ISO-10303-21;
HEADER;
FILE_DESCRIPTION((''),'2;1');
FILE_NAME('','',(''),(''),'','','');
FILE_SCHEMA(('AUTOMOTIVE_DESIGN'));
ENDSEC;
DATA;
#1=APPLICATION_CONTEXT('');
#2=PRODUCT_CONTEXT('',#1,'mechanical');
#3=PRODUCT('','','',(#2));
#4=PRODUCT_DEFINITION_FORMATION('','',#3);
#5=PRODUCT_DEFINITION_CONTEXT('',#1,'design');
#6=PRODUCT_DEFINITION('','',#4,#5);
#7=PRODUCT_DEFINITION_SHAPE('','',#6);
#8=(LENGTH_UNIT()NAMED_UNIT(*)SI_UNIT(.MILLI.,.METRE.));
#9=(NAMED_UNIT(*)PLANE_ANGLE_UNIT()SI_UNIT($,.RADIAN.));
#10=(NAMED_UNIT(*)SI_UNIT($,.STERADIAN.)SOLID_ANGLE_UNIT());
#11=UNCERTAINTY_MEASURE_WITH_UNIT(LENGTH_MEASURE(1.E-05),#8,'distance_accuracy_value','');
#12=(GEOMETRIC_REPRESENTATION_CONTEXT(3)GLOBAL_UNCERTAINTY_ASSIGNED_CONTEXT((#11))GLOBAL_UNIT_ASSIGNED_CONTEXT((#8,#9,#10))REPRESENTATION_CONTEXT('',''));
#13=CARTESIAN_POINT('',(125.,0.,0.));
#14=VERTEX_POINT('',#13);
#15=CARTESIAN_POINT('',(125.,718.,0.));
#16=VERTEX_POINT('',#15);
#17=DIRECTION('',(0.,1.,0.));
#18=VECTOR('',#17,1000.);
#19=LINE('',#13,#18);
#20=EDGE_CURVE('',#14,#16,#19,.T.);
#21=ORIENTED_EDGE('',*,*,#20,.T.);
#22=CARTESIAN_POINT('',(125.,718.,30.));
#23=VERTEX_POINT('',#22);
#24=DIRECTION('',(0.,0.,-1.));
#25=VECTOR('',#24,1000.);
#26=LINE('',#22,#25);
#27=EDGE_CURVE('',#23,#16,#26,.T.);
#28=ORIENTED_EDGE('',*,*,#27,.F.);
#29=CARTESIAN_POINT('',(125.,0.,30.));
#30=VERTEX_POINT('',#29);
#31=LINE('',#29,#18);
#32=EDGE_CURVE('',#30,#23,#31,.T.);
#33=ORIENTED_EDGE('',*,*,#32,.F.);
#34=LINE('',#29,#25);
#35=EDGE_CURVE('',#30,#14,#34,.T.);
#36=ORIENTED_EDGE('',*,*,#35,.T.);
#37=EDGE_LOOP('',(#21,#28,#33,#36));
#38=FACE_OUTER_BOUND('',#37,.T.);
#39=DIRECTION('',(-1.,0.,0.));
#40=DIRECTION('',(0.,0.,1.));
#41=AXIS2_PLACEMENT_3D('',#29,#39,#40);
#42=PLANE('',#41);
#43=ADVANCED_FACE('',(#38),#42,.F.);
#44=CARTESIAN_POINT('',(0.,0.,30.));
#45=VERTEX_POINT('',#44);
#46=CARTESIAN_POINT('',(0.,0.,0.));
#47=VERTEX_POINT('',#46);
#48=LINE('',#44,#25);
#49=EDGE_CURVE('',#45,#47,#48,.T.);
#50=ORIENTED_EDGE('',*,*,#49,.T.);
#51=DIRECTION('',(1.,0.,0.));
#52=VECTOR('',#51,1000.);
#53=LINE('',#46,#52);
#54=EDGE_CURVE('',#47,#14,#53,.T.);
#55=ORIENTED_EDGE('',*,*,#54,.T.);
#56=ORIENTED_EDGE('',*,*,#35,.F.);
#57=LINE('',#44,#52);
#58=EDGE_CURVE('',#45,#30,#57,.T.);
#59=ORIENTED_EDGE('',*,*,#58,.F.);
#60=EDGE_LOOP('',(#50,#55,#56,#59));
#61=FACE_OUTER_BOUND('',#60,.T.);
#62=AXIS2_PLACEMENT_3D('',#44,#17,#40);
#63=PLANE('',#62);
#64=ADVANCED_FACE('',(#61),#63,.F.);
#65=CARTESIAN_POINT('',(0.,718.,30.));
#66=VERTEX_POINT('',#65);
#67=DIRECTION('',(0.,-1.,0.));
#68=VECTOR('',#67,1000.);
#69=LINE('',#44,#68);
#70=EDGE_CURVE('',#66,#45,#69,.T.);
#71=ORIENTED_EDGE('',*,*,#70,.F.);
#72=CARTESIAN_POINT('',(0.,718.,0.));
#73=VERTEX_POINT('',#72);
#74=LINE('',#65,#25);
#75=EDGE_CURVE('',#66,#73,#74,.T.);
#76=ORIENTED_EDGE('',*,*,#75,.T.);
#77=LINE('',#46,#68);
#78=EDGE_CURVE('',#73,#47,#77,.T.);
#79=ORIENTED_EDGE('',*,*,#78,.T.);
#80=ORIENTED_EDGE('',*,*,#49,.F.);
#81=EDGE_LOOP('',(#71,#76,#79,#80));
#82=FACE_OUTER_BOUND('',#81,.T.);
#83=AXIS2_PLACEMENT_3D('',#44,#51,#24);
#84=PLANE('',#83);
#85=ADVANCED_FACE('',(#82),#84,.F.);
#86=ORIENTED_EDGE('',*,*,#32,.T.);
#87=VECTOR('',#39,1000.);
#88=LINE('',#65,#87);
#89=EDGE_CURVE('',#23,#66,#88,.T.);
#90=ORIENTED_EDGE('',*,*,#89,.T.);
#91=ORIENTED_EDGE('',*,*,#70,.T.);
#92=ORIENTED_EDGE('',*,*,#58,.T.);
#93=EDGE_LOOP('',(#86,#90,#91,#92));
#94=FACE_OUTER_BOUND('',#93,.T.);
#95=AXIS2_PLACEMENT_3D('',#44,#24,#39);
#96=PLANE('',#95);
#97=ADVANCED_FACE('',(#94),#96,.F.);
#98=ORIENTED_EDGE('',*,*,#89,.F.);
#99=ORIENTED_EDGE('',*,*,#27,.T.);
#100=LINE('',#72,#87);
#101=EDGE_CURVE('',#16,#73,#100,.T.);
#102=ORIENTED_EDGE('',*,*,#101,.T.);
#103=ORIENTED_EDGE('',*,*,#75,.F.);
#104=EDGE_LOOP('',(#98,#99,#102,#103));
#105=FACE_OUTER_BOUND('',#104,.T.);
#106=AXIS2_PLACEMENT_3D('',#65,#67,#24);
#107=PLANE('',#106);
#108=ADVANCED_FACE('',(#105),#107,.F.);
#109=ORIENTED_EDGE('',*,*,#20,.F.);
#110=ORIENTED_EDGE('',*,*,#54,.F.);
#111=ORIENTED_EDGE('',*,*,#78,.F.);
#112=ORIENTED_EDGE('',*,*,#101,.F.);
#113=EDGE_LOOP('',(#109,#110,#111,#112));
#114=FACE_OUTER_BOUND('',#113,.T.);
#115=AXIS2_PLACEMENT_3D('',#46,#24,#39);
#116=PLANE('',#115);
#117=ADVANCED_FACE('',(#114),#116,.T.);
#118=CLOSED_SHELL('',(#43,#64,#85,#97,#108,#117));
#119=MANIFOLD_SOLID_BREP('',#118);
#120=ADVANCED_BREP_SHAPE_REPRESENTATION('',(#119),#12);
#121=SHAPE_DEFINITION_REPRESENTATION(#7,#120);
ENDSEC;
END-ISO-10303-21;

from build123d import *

# Parameters (mm, degrees)
SKETCH1_W           = 125
SKETCH1_H           = 718
BOSS_EXTRUDE1_DEPTH = 30


with BuildPart() as part:
    # Sketch1 → Boss-Extrude1 (new body)
    with BuildSketch(Plane.XY):
        with Locations((62.5, 359)):
            Rectangle(SKETCH1_W, SKETCH1_H)
    extrude(amount=BOSS_EXTRUDE1_DEPTH)


solid = part.part
